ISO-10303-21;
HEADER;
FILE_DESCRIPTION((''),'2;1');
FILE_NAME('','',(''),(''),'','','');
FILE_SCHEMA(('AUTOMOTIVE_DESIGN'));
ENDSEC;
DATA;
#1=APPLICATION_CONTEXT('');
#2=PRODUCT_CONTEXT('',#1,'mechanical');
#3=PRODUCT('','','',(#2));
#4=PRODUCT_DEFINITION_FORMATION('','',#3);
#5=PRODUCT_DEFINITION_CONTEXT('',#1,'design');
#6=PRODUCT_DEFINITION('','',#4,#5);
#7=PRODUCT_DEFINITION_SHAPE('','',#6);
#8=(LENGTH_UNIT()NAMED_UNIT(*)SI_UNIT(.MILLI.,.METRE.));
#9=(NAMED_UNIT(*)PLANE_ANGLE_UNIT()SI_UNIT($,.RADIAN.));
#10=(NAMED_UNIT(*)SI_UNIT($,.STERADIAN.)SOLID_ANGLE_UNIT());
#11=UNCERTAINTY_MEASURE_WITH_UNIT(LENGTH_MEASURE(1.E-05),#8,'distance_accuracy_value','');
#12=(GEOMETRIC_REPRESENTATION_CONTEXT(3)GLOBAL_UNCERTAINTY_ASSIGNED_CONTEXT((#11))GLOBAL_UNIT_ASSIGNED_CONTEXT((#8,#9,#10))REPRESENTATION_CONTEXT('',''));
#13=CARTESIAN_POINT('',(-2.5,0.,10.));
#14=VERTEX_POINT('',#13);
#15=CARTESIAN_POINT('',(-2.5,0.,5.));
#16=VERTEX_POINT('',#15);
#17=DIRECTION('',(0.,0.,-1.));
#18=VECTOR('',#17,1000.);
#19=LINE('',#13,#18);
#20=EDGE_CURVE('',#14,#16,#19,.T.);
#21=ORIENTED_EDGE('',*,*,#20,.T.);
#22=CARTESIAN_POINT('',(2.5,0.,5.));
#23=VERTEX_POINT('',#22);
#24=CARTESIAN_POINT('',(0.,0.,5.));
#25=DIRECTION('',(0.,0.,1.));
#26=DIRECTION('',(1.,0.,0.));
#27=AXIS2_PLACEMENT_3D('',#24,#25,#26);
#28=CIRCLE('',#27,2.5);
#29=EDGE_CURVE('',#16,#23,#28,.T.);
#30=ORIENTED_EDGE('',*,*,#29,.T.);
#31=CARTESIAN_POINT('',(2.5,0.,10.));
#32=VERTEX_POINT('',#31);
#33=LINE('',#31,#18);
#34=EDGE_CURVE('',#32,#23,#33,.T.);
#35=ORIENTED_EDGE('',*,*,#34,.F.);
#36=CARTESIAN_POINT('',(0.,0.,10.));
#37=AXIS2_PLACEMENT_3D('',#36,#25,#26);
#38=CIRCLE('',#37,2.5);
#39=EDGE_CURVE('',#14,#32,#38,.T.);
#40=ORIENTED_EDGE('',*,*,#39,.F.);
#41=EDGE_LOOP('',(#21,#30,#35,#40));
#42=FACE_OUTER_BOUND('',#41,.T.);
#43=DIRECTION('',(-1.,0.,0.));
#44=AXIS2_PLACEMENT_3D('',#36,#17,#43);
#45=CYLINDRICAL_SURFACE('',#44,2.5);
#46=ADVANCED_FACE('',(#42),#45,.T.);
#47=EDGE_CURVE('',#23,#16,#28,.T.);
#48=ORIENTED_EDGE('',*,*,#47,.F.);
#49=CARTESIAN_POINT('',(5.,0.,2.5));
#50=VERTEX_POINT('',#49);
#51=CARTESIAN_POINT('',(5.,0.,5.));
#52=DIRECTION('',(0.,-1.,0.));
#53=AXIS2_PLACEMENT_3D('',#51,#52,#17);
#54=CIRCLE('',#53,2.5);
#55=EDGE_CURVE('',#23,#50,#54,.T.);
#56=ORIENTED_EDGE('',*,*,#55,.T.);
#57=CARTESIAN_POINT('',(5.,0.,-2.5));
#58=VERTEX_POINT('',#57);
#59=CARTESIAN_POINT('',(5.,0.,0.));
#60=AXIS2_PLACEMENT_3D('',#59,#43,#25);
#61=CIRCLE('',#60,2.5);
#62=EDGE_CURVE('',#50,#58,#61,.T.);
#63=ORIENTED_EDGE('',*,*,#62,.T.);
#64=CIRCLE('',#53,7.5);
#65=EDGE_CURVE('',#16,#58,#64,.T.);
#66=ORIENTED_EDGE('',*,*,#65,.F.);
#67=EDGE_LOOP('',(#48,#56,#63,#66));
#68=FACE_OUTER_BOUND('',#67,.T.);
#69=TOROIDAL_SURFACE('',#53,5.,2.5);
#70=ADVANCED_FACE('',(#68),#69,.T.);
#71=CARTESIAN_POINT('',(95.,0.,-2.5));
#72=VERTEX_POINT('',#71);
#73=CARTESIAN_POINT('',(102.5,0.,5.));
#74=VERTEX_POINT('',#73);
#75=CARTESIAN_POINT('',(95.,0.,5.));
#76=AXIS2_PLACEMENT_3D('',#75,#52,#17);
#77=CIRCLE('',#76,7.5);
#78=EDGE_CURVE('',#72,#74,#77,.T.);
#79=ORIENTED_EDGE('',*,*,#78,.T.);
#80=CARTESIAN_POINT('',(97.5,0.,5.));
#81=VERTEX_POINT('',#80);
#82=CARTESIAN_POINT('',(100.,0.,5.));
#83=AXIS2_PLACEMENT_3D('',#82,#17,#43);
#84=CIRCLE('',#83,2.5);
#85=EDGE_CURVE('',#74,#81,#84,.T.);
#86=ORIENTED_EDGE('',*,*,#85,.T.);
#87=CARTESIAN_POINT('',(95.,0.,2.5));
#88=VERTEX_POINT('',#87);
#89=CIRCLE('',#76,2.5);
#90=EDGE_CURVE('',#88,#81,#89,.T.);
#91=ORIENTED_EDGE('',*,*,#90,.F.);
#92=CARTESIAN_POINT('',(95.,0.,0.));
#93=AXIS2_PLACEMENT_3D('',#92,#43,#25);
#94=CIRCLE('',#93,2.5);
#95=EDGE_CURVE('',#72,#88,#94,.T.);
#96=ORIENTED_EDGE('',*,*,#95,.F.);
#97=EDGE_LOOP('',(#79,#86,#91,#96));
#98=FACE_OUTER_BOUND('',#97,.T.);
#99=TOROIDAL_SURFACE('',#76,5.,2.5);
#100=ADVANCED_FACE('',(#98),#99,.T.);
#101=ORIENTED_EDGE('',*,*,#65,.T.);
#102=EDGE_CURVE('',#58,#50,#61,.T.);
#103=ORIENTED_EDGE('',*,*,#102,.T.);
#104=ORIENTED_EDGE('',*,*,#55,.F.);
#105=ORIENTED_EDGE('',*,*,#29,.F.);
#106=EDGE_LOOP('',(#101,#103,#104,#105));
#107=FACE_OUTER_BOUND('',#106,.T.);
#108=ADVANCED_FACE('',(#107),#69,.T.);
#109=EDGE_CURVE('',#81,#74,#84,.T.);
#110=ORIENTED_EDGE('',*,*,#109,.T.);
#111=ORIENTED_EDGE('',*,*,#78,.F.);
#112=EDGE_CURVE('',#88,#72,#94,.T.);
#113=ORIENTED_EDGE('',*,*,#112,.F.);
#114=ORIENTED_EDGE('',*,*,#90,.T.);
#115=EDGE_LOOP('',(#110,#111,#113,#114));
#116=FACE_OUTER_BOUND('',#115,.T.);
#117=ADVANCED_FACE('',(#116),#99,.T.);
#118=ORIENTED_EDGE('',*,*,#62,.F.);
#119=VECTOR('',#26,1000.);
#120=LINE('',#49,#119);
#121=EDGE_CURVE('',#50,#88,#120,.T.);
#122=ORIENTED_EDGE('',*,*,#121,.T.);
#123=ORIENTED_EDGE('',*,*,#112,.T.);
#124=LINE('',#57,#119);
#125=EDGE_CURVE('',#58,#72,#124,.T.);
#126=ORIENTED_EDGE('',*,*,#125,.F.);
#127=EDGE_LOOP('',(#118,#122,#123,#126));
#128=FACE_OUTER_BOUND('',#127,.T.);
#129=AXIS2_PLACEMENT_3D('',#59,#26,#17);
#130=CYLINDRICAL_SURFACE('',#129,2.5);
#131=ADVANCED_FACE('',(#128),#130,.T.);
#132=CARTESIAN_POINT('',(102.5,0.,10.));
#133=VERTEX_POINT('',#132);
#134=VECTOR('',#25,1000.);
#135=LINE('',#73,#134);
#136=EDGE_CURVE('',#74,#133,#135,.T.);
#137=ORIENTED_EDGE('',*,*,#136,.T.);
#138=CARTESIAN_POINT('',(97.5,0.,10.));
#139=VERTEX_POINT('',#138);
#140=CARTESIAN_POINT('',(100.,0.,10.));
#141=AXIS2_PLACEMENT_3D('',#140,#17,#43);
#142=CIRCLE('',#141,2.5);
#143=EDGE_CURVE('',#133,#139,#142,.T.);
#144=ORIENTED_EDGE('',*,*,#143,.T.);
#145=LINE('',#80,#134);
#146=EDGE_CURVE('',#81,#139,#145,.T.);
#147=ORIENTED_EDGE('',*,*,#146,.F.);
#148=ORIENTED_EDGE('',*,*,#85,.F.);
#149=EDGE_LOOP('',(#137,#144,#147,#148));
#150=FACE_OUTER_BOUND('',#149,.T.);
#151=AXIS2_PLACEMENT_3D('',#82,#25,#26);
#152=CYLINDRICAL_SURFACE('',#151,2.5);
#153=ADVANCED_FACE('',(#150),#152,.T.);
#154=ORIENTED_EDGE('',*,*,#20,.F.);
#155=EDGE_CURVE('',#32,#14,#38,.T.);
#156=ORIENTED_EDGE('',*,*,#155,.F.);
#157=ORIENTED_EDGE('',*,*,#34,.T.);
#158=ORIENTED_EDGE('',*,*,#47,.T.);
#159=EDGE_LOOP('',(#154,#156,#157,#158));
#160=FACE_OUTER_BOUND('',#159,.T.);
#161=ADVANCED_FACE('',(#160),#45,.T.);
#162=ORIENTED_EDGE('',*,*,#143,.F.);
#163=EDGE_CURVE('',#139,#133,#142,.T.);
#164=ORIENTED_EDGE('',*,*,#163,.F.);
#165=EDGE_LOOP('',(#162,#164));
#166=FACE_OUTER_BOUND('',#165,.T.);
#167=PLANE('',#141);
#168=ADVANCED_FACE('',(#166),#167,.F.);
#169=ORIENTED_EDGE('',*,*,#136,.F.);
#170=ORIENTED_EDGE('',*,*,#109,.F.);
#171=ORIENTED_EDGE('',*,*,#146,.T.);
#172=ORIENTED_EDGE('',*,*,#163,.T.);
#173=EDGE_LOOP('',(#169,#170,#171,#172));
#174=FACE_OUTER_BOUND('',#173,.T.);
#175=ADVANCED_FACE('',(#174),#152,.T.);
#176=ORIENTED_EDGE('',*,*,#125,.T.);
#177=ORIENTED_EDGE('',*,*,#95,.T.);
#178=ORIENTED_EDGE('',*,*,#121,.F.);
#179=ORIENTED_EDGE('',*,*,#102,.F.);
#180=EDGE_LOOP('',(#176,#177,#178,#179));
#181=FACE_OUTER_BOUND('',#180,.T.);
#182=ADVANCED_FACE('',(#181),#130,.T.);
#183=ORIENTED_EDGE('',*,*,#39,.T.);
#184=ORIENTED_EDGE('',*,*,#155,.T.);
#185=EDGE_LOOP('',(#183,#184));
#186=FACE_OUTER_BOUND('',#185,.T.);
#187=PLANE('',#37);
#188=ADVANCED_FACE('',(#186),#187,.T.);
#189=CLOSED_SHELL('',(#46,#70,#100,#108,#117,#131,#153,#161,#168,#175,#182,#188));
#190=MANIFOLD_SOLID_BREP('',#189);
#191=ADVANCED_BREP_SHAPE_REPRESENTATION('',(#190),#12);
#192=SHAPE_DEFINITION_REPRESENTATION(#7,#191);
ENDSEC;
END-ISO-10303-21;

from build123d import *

# Parameters (mm, degrees)
SWEEP1_PROFILE_R = 2.5


with BuildPart() as part:
    # Sweep1: sweep along a path in Sketch1
    with BuildLine(Plane(origin=(0, 0, 0), x_dir=(1, 0, 0), z_dir=(0, 1, 0))) as sweep1_path:
        Line((0, -10), (0, -5))
        ThreePointArc((0, -5), (1.464466094, -1.464466094), (5, 0))
        Line((5, 0), (95, 0))
        ThreePointArc((95, 0), (98.535533906, -1.464466094), (100, -5))
        Line((100, -5), (100, -10))
    # Sweep1 profile (on start of the path) → Sweep1 (sweep)
    with BuildSketch(Plane(origin=(0, 0, 10), x_dir=(-1, 0, 0), z_dir=(0, 0, -1))):
        Circle(SWEEP1_PROFILE_R)
    sweep(path=sweep1_path.line)


solid = part.part
